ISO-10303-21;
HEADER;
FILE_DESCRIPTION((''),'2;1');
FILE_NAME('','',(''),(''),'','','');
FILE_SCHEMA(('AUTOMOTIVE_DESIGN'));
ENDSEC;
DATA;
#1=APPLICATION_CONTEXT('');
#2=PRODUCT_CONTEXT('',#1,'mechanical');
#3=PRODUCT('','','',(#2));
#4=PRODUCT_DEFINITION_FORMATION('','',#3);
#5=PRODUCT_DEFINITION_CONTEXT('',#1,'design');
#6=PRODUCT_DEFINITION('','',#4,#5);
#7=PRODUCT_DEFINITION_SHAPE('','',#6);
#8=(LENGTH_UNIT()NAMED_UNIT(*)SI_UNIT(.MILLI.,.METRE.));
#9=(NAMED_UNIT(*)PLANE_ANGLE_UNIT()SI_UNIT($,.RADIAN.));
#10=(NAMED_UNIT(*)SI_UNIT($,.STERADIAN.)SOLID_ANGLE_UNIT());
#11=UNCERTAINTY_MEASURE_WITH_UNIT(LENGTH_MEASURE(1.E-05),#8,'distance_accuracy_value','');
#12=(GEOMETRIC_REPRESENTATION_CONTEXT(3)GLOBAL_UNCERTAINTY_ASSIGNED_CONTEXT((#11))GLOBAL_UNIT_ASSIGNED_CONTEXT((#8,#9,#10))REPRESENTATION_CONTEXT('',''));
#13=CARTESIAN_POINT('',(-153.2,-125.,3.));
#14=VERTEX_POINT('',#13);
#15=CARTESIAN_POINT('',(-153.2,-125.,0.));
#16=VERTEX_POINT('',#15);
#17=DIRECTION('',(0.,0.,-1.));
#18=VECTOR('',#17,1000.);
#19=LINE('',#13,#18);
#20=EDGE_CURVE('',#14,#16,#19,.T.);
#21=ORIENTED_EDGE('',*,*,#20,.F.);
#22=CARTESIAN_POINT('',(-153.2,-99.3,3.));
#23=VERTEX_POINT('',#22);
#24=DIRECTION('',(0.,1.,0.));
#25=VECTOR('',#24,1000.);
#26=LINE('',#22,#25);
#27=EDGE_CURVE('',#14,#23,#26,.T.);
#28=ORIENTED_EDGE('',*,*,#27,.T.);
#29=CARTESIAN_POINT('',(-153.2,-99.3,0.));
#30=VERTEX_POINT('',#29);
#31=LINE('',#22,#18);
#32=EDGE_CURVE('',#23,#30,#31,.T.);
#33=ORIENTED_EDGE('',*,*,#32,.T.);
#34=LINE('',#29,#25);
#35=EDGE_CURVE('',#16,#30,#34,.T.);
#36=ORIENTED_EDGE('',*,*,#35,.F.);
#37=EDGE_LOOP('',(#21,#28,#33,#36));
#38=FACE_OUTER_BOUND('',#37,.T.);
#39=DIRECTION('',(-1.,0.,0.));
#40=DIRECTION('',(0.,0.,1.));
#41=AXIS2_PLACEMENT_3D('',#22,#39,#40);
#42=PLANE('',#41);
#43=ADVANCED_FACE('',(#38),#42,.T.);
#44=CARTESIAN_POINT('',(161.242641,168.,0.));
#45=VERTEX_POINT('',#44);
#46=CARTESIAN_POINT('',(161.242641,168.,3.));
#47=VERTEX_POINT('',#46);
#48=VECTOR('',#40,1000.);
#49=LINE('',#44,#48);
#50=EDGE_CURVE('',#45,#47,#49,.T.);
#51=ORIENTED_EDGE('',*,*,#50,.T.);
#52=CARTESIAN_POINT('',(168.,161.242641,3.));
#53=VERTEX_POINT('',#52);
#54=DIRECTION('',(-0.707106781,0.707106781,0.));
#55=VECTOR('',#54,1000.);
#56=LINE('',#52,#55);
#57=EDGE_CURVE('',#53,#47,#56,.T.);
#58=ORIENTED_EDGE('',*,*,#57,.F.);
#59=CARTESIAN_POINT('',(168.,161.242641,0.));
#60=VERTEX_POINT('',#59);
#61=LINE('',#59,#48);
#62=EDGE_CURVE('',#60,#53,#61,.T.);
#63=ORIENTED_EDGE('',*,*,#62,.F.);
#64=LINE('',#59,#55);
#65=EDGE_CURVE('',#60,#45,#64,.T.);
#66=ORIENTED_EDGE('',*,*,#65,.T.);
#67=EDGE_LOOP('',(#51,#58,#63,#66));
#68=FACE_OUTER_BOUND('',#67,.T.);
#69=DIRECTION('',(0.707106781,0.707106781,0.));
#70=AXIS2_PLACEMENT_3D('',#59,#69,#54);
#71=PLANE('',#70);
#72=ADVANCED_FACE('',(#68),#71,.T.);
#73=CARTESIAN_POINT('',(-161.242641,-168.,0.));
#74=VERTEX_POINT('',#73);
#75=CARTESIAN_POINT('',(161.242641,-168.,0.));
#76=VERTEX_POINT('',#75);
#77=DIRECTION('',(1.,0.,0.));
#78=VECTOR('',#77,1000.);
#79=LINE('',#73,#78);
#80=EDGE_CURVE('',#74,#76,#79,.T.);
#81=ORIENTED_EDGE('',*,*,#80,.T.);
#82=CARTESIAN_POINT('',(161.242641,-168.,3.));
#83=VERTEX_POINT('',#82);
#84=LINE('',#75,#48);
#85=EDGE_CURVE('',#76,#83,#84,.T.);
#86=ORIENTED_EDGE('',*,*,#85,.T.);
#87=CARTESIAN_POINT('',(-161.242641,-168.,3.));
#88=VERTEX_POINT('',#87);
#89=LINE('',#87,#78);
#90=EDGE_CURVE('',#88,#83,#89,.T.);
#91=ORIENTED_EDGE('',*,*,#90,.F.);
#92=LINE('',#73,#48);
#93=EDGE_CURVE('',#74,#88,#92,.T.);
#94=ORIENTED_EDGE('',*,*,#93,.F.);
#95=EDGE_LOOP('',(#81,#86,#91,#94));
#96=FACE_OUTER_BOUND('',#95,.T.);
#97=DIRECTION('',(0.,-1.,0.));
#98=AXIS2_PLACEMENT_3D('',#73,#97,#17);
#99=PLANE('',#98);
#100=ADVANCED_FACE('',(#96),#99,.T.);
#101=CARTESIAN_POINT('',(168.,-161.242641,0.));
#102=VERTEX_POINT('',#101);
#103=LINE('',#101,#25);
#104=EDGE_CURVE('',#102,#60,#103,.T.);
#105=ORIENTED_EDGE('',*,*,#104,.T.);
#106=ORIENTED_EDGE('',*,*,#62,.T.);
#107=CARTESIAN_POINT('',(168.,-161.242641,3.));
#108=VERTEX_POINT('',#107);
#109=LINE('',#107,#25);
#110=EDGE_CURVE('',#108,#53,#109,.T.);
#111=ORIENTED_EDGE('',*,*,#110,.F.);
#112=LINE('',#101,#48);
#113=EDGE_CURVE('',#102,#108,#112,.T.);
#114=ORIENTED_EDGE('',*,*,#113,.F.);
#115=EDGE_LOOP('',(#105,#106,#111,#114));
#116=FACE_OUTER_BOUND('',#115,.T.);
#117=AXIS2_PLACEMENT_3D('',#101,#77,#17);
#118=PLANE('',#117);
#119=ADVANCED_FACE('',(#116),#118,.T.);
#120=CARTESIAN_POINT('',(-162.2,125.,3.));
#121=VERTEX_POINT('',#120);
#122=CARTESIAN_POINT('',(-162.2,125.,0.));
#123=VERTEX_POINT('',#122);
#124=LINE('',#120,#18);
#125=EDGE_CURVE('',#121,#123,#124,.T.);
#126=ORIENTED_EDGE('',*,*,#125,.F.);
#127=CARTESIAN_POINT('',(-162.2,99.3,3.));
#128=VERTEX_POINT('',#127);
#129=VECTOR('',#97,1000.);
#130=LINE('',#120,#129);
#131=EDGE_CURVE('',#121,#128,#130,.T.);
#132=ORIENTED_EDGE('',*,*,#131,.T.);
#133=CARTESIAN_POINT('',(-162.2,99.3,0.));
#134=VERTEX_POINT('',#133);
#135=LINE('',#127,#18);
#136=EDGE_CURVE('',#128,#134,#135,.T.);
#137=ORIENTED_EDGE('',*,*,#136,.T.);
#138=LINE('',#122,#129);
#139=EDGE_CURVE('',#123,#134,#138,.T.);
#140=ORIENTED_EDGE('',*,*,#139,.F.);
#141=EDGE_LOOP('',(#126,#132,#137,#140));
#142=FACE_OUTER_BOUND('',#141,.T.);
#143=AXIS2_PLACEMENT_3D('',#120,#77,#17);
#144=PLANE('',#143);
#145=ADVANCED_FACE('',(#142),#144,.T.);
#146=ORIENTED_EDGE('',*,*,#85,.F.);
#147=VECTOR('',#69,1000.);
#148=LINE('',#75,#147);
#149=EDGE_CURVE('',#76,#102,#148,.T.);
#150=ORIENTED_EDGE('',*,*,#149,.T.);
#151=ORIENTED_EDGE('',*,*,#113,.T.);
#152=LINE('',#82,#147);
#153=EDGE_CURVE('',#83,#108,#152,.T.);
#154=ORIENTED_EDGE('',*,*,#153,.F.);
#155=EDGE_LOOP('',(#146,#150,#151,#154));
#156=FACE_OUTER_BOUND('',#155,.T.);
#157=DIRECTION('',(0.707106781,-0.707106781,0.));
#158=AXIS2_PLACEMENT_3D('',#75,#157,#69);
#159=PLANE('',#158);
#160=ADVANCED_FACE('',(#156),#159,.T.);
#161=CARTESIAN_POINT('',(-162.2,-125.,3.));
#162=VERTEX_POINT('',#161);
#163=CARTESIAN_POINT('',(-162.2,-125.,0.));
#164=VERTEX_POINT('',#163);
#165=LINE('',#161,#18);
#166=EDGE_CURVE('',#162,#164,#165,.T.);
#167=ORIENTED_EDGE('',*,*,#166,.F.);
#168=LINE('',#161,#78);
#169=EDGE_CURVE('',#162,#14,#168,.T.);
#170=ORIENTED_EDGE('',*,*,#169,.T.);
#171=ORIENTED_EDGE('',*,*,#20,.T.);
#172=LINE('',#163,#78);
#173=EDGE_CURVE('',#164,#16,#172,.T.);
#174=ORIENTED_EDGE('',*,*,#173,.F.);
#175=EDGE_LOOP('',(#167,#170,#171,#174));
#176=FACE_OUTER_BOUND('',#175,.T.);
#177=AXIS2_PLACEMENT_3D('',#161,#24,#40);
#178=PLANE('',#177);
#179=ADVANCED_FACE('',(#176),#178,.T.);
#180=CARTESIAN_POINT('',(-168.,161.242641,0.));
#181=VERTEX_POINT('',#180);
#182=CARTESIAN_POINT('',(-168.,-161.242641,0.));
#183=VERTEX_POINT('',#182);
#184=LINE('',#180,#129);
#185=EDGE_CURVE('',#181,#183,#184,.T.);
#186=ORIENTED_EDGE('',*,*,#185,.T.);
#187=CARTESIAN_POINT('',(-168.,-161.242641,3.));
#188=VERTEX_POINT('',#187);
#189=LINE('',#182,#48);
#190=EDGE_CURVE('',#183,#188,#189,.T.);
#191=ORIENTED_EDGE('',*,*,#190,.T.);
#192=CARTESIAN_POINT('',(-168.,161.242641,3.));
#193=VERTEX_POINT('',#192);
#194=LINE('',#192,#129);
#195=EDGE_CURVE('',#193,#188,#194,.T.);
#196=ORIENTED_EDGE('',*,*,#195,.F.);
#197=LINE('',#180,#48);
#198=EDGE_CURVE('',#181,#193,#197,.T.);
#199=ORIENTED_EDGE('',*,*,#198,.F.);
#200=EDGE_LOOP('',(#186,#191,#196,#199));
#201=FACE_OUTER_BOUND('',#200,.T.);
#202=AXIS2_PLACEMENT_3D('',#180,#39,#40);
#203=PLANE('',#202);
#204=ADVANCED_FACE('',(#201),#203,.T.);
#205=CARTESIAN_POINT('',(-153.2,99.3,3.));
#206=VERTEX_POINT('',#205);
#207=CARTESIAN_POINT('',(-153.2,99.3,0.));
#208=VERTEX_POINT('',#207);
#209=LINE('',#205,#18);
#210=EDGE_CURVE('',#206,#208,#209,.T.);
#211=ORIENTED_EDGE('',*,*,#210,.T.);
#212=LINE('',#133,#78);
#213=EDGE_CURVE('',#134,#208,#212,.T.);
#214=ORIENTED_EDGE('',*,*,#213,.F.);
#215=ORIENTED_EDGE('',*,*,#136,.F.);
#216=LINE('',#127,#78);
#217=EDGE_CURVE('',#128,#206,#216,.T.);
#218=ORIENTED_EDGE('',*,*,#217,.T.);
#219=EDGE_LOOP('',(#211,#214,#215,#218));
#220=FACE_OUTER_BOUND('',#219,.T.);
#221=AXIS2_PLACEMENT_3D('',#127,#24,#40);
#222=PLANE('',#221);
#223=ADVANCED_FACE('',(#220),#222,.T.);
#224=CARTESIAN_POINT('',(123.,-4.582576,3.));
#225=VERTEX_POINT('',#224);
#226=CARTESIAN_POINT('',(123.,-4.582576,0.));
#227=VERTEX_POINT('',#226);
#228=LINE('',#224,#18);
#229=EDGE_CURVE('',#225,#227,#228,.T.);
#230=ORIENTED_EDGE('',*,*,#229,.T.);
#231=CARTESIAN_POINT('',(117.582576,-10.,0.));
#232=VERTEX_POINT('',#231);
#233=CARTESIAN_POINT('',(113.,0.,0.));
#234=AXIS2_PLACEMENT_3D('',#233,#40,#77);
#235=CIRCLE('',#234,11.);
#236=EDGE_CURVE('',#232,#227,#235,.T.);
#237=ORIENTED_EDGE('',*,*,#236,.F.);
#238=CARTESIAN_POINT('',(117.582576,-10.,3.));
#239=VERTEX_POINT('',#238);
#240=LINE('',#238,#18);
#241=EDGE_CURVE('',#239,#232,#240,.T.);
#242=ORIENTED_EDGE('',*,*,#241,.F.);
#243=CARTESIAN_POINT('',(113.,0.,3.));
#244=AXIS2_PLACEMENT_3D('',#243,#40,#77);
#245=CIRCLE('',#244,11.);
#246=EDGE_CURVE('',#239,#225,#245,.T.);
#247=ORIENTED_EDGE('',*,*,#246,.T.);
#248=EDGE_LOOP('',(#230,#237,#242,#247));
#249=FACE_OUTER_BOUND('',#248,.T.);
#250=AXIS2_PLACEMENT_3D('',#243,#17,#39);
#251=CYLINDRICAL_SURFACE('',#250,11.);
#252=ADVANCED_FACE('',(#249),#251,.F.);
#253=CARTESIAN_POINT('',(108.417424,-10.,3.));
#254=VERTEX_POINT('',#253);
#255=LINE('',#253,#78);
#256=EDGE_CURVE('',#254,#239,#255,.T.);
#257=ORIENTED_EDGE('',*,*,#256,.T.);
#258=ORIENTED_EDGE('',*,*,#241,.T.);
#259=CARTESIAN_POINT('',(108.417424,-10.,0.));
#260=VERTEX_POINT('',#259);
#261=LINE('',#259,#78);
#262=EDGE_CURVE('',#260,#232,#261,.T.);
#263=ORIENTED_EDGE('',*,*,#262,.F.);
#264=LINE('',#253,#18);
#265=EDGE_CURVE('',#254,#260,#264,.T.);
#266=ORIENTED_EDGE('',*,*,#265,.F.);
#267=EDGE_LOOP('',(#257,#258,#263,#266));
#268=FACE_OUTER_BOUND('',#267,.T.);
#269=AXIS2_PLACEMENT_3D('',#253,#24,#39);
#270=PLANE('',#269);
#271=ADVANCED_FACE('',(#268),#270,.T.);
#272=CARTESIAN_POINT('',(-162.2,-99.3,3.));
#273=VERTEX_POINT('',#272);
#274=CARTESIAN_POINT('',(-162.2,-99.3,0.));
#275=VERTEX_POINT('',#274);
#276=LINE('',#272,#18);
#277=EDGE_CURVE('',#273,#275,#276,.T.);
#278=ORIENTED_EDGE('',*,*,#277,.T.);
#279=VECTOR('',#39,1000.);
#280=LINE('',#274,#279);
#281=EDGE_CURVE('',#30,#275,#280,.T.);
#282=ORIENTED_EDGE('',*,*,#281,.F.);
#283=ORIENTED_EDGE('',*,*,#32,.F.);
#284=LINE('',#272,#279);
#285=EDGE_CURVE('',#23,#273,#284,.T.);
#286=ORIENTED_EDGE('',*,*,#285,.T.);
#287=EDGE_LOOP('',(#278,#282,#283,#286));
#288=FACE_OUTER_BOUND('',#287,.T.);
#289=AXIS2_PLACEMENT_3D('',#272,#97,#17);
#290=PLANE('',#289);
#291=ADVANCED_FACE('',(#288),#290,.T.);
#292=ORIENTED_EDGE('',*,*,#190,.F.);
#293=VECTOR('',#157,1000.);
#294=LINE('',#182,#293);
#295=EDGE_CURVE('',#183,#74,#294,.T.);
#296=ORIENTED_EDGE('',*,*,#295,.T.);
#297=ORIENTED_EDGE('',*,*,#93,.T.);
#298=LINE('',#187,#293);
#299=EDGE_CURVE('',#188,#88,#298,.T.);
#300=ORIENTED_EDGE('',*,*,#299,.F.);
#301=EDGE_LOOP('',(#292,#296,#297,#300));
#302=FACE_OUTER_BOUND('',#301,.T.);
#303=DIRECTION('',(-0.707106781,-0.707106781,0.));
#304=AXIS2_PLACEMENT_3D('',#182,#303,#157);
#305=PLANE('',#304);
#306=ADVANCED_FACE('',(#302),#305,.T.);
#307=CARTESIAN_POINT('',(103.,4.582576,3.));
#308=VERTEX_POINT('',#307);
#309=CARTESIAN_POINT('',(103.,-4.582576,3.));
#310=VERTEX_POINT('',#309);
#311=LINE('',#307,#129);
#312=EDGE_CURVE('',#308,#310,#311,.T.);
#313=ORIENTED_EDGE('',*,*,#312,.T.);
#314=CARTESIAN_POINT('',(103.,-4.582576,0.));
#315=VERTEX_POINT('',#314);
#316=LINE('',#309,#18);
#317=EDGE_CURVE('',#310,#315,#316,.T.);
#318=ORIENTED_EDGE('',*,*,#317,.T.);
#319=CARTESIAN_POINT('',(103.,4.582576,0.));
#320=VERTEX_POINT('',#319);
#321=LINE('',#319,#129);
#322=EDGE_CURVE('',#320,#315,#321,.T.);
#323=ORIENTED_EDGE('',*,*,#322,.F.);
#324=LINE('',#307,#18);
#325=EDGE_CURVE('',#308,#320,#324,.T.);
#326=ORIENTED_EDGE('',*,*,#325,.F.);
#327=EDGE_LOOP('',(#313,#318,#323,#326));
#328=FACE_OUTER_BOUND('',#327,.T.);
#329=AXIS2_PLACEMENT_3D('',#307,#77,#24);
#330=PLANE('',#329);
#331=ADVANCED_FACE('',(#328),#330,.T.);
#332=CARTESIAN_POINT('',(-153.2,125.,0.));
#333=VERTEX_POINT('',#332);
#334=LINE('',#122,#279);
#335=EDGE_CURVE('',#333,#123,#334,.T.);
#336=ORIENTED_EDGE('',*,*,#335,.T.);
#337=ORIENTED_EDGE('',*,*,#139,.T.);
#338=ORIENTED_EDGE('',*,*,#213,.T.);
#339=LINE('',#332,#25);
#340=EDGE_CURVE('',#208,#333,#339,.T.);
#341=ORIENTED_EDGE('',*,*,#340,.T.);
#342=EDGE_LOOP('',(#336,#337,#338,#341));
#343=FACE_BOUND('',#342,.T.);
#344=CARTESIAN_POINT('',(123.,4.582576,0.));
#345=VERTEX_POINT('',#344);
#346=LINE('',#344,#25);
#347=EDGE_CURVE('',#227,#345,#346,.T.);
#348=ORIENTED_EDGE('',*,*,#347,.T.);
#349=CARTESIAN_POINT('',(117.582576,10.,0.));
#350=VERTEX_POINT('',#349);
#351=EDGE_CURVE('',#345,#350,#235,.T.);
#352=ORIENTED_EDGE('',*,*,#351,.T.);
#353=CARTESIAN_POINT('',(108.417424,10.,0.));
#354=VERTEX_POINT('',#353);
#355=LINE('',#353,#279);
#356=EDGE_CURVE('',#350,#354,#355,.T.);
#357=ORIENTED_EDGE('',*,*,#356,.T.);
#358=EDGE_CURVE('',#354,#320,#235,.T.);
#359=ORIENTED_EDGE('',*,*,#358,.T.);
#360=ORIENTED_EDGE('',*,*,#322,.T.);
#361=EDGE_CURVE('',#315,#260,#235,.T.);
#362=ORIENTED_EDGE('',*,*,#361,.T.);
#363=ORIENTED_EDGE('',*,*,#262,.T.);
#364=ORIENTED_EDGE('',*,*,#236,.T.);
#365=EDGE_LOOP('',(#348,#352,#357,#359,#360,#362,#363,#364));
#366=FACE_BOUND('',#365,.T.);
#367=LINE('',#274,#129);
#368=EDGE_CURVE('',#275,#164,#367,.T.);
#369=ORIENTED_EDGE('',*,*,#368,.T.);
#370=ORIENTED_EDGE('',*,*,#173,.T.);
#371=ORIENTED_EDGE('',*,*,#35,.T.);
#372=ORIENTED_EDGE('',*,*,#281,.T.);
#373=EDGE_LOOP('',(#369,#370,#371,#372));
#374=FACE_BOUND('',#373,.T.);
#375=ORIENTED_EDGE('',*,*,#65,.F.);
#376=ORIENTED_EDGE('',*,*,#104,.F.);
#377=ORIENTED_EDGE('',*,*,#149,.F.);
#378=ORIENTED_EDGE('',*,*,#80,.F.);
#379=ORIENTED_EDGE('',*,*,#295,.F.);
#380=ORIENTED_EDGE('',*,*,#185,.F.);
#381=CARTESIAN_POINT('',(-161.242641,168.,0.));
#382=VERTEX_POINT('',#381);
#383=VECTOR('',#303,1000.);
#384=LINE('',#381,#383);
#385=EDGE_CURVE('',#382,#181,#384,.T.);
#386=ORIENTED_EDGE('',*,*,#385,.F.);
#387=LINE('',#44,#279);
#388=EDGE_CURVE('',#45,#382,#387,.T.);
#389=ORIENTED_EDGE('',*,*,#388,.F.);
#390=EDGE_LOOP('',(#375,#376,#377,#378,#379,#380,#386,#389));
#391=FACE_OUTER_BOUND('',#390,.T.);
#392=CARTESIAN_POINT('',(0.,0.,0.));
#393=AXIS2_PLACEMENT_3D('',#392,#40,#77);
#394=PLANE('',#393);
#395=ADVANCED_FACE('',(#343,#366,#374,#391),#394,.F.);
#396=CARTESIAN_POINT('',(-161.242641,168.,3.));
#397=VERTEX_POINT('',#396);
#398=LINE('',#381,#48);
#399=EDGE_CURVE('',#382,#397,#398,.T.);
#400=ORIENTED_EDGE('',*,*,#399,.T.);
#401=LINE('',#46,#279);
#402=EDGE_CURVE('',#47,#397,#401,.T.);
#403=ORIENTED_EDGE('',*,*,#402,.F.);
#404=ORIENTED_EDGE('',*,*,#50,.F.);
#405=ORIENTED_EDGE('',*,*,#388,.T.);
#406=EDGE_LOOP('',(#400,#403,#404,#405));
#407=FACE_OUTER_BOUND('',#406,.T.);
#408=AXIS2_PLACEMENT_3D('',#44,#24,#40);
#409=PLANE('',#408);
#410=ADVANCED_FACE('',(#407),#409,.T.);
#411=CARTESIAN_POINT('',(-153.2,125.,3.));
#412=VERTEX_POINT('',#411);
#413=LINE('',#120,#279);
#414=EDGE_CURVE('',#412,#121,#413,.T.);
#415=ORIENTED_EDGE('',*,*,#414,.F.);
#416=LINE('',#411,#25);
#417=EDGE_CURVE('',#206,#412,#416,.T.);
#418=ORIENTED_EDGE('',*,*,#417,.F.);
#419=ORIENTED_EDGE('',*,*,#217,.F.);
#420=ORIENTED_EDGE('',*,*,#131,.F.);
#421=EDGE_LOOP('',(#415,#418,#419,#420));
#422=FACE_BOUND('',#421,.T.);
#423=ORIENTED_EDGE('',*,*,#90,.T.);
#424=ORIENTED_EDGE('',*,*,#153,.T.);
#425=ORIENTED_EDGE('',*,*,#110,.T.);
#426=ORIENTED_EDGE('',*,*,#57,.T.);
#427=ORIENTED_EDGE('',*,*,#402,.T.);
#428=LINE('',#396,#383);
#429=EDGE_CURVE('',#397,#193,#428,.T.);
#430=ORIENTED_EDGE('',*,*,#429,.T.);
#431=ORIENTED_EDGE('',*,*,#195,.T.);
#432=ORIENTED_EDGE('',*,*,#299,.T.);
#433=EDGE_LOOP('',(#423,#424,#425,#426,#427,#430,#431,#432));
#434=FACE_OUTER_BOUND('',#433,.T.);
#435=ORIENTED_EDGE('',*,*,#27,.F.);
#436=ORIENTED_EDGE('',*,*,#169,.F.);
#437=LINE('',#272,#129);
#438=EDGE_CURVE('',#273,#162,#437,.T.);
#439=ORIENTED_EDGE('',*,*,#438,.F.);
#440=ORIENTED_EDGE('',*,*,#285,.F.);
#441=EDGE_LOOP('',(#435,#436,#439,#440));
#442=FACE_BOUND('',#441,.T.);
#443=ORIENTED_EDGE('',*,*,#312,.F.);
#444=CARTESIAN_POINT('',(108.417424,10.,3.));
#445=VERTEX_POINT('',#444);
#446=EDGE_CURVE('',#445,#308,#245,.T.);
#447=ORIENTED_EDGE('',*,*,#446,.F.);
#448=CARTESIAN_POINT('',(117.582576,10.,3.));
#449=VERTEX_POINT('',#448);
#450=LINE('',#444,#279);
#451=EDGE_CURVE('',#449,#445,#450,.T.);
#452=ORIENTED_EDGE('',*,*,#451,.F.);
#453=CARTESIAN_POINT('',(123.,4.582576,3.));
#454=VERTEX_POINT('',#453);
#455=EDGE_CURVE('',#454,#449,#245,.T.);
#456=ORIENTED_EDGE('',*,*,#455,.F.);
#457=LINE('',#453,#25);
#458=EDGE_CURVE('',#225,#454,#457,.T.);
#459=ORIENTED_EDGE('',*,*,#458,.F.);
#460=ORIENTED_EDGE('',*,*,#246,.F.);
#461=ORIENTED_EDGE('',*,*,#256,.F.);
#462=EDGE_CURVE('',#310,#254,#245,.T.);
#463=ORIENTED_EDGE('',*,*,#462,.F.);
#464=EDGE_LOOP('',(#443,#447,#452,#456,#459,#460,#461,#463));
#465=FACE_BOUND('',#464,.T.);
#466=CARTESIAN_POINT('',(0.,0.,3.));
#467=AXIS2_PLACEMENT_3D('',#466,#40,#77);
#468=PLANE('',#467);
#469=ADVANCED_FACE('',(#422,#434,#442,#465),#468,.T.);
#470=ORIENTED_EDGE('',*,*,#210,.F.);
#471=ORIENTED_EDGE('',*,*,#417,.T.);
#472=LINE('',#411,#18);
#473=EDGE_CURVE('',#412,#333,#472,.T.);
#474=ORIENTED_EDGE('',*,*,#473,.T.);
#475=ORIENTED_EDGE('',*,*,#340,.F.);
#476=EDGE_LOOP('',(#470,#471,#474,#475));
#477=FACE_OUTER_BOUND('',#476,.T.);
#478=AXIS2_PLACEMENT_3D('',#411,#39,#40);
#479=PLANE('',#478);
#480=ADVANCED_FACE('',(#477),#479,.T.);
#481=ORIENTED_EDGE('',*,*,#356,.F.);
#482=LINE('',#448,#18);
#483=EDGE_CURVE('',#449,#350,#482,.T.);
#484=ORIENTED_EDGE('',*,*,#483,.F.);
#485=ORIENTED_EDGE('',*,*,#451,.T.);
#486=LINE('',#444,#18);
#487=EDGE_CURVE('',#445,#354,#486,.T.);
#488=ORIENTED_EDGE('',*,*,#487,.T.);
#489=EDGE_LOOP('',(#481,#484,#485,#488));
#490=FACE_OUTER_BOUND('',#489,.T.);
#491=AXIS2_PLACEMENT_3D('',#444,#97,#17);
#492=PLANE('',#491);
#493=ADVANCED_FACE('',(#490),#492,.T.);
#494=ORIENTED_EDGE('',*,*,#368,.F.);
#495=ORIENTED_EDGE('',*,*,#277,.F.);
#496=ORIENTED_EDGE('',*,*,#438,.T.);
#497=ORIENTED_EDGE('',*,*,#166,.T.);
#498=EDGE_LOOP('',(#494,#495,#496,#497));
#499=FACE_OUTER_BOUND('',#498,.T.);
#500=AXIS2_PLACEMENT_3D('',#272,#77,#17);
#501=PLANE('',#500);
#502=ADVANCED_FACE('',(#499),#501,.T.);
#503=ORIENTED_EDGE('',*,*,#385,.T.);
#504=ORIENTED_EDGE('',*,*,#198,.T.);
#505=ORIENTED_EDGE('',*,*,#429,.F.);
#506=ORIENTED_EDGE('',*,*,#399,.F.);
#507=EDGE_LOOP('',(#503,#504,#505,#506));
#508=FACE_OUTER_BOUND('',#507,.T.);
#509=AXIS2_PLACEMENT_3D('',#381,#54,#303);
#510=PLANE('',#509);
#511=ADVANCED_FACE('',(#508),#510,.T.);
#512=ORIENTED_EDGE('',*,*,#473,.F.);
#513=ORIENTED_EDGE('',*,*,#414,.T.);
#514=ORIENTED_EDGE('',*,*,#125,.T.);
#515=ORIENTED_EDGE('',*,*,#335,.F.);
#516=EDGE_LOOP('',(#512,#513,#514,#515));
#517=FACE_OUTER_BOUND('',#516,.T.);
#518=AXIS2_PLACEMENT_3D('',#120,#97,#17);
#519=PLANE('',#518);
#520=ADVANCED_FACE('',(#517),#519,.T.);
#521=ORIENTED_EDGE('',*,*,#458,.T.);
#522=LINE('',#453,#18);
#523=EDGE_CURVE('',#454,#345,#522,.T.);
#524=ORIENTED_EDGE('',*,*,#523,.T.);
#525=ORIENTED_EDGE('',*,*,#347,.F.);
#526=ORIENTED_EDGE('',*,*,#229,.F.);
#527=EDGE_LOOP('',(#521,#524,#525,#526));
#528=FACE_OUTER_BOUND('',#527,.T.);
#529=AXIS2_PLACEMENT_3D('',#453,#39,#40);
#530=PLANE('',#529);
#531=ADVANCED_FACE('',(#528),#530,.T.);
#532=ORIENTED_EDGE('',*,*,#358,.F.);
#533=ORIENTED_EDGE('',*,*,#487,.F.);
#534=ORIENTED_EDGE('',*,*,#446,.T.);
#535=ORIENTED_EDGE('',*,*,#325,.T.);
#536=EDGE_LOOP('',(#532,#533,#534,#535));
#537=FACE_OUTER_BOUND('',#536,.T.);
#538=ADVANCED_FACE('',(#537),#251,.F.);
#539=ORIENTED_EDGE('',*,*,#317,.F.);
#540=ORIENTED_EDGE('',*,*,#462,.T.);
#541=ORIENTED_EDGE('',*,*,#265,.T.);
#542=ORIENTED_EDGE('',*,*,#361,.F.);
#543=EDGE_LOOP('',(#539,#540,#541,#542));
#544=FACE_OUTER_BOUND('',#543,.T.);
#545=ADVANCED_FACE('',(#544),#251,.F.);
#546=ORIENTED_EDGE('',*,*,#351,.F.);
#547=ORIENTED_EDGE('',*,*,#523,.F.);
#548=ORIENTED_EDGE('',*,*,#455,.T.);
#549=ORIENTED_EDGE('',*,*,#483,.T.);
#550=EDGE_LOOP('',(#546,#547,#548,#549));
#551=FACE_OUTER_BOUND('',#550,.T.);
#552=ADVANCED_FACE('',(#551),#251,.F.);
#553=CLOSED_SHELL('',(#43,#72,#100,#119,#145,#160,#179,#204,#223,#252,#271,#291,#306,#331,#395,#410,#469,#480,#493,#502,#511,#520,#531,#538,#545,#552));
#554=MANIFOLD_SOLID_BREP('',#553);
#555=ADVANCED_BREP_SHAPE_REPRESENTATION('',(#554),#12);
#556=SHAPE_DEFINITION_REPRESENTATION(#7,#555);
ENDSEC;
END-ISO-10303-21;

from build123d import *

# Parameters (mm, degrees)
SKETCH1_W           = 9
SKETCH1_H           = 25.7
BOSS_EXTRUDE1_DEPTH = 3
BOSS_EXTRUDE2_DEPTH = 3


with BuildPart() as part:
    # Sketch1 → Boss-Extrude1 (new body)
    with BuildSketch(Plane.XY):
        Polygon((165, -160), (165, 160), (160, 165), (-160, 165), (-165, 160), (-165, -160), (-160, -165), (160, -165), align=None)
        with BuildLine():
            Line((108.417424305, 10), (117.582575695, 10))
            ThreePointArc((117.582575695, 10), (120.778174593, 7.778174593), (123, 4.582575695))
            Line((123, 4.582575695), (123, -4.582575695))
            ThreePointArc((123, -4.582575695), (120.778174593, -7.778174593), (117.582575695, -10))
            Line((117.582575695, -10), (108.417424305, -10))
            ThreePointArc((108.417424305, -10), (105.221825407, -7.778174593), (103, -4.582575695))
            Line((103, -4.582575695), (103, 4.582575695))
            ThreePointArc((103, 4.582575695), (105.221825407, 7.778174593), (108.417424305, 10))
        make_face(mode=Mode.SUBTRACT)
        with Locations((-157.7, 112.15)):
            Rectangle(SKETCH1_W, SKETCH1_H, mode=Mode.SUBTRACT)
        with Locations((-157.7, -112.15)):
            Rectangle(SKETCH1_W, SKETCH1_H, mode=Mode.SUBTRACT)
    extrude(amount=BOSS_EXTRUDE1_DEPTH)

    # Sketch2 → Boss-Extrude2 (add)
    with BuildSketch(Plane.XY.offset(3)):
        Polygon((168, -161.242640687), (168, 161.242640687), (161.242640687, 168), (-161.242640687, 168), (-168, 161.242640687), (-168, -161.242640687), (-161.242640687, -168), (161.242640687, -168), align=None)
        Polygon((160, -165), (165, -160), (165, 160), (160, 165), (-160, 165), (-165, 160), (-165, -160), (-160, -165), align=None, mode=Mode.SUBTRACT)
    extrude(amount=-BOSS_EXTRUDE2_DEPTH)


solid = part.part
